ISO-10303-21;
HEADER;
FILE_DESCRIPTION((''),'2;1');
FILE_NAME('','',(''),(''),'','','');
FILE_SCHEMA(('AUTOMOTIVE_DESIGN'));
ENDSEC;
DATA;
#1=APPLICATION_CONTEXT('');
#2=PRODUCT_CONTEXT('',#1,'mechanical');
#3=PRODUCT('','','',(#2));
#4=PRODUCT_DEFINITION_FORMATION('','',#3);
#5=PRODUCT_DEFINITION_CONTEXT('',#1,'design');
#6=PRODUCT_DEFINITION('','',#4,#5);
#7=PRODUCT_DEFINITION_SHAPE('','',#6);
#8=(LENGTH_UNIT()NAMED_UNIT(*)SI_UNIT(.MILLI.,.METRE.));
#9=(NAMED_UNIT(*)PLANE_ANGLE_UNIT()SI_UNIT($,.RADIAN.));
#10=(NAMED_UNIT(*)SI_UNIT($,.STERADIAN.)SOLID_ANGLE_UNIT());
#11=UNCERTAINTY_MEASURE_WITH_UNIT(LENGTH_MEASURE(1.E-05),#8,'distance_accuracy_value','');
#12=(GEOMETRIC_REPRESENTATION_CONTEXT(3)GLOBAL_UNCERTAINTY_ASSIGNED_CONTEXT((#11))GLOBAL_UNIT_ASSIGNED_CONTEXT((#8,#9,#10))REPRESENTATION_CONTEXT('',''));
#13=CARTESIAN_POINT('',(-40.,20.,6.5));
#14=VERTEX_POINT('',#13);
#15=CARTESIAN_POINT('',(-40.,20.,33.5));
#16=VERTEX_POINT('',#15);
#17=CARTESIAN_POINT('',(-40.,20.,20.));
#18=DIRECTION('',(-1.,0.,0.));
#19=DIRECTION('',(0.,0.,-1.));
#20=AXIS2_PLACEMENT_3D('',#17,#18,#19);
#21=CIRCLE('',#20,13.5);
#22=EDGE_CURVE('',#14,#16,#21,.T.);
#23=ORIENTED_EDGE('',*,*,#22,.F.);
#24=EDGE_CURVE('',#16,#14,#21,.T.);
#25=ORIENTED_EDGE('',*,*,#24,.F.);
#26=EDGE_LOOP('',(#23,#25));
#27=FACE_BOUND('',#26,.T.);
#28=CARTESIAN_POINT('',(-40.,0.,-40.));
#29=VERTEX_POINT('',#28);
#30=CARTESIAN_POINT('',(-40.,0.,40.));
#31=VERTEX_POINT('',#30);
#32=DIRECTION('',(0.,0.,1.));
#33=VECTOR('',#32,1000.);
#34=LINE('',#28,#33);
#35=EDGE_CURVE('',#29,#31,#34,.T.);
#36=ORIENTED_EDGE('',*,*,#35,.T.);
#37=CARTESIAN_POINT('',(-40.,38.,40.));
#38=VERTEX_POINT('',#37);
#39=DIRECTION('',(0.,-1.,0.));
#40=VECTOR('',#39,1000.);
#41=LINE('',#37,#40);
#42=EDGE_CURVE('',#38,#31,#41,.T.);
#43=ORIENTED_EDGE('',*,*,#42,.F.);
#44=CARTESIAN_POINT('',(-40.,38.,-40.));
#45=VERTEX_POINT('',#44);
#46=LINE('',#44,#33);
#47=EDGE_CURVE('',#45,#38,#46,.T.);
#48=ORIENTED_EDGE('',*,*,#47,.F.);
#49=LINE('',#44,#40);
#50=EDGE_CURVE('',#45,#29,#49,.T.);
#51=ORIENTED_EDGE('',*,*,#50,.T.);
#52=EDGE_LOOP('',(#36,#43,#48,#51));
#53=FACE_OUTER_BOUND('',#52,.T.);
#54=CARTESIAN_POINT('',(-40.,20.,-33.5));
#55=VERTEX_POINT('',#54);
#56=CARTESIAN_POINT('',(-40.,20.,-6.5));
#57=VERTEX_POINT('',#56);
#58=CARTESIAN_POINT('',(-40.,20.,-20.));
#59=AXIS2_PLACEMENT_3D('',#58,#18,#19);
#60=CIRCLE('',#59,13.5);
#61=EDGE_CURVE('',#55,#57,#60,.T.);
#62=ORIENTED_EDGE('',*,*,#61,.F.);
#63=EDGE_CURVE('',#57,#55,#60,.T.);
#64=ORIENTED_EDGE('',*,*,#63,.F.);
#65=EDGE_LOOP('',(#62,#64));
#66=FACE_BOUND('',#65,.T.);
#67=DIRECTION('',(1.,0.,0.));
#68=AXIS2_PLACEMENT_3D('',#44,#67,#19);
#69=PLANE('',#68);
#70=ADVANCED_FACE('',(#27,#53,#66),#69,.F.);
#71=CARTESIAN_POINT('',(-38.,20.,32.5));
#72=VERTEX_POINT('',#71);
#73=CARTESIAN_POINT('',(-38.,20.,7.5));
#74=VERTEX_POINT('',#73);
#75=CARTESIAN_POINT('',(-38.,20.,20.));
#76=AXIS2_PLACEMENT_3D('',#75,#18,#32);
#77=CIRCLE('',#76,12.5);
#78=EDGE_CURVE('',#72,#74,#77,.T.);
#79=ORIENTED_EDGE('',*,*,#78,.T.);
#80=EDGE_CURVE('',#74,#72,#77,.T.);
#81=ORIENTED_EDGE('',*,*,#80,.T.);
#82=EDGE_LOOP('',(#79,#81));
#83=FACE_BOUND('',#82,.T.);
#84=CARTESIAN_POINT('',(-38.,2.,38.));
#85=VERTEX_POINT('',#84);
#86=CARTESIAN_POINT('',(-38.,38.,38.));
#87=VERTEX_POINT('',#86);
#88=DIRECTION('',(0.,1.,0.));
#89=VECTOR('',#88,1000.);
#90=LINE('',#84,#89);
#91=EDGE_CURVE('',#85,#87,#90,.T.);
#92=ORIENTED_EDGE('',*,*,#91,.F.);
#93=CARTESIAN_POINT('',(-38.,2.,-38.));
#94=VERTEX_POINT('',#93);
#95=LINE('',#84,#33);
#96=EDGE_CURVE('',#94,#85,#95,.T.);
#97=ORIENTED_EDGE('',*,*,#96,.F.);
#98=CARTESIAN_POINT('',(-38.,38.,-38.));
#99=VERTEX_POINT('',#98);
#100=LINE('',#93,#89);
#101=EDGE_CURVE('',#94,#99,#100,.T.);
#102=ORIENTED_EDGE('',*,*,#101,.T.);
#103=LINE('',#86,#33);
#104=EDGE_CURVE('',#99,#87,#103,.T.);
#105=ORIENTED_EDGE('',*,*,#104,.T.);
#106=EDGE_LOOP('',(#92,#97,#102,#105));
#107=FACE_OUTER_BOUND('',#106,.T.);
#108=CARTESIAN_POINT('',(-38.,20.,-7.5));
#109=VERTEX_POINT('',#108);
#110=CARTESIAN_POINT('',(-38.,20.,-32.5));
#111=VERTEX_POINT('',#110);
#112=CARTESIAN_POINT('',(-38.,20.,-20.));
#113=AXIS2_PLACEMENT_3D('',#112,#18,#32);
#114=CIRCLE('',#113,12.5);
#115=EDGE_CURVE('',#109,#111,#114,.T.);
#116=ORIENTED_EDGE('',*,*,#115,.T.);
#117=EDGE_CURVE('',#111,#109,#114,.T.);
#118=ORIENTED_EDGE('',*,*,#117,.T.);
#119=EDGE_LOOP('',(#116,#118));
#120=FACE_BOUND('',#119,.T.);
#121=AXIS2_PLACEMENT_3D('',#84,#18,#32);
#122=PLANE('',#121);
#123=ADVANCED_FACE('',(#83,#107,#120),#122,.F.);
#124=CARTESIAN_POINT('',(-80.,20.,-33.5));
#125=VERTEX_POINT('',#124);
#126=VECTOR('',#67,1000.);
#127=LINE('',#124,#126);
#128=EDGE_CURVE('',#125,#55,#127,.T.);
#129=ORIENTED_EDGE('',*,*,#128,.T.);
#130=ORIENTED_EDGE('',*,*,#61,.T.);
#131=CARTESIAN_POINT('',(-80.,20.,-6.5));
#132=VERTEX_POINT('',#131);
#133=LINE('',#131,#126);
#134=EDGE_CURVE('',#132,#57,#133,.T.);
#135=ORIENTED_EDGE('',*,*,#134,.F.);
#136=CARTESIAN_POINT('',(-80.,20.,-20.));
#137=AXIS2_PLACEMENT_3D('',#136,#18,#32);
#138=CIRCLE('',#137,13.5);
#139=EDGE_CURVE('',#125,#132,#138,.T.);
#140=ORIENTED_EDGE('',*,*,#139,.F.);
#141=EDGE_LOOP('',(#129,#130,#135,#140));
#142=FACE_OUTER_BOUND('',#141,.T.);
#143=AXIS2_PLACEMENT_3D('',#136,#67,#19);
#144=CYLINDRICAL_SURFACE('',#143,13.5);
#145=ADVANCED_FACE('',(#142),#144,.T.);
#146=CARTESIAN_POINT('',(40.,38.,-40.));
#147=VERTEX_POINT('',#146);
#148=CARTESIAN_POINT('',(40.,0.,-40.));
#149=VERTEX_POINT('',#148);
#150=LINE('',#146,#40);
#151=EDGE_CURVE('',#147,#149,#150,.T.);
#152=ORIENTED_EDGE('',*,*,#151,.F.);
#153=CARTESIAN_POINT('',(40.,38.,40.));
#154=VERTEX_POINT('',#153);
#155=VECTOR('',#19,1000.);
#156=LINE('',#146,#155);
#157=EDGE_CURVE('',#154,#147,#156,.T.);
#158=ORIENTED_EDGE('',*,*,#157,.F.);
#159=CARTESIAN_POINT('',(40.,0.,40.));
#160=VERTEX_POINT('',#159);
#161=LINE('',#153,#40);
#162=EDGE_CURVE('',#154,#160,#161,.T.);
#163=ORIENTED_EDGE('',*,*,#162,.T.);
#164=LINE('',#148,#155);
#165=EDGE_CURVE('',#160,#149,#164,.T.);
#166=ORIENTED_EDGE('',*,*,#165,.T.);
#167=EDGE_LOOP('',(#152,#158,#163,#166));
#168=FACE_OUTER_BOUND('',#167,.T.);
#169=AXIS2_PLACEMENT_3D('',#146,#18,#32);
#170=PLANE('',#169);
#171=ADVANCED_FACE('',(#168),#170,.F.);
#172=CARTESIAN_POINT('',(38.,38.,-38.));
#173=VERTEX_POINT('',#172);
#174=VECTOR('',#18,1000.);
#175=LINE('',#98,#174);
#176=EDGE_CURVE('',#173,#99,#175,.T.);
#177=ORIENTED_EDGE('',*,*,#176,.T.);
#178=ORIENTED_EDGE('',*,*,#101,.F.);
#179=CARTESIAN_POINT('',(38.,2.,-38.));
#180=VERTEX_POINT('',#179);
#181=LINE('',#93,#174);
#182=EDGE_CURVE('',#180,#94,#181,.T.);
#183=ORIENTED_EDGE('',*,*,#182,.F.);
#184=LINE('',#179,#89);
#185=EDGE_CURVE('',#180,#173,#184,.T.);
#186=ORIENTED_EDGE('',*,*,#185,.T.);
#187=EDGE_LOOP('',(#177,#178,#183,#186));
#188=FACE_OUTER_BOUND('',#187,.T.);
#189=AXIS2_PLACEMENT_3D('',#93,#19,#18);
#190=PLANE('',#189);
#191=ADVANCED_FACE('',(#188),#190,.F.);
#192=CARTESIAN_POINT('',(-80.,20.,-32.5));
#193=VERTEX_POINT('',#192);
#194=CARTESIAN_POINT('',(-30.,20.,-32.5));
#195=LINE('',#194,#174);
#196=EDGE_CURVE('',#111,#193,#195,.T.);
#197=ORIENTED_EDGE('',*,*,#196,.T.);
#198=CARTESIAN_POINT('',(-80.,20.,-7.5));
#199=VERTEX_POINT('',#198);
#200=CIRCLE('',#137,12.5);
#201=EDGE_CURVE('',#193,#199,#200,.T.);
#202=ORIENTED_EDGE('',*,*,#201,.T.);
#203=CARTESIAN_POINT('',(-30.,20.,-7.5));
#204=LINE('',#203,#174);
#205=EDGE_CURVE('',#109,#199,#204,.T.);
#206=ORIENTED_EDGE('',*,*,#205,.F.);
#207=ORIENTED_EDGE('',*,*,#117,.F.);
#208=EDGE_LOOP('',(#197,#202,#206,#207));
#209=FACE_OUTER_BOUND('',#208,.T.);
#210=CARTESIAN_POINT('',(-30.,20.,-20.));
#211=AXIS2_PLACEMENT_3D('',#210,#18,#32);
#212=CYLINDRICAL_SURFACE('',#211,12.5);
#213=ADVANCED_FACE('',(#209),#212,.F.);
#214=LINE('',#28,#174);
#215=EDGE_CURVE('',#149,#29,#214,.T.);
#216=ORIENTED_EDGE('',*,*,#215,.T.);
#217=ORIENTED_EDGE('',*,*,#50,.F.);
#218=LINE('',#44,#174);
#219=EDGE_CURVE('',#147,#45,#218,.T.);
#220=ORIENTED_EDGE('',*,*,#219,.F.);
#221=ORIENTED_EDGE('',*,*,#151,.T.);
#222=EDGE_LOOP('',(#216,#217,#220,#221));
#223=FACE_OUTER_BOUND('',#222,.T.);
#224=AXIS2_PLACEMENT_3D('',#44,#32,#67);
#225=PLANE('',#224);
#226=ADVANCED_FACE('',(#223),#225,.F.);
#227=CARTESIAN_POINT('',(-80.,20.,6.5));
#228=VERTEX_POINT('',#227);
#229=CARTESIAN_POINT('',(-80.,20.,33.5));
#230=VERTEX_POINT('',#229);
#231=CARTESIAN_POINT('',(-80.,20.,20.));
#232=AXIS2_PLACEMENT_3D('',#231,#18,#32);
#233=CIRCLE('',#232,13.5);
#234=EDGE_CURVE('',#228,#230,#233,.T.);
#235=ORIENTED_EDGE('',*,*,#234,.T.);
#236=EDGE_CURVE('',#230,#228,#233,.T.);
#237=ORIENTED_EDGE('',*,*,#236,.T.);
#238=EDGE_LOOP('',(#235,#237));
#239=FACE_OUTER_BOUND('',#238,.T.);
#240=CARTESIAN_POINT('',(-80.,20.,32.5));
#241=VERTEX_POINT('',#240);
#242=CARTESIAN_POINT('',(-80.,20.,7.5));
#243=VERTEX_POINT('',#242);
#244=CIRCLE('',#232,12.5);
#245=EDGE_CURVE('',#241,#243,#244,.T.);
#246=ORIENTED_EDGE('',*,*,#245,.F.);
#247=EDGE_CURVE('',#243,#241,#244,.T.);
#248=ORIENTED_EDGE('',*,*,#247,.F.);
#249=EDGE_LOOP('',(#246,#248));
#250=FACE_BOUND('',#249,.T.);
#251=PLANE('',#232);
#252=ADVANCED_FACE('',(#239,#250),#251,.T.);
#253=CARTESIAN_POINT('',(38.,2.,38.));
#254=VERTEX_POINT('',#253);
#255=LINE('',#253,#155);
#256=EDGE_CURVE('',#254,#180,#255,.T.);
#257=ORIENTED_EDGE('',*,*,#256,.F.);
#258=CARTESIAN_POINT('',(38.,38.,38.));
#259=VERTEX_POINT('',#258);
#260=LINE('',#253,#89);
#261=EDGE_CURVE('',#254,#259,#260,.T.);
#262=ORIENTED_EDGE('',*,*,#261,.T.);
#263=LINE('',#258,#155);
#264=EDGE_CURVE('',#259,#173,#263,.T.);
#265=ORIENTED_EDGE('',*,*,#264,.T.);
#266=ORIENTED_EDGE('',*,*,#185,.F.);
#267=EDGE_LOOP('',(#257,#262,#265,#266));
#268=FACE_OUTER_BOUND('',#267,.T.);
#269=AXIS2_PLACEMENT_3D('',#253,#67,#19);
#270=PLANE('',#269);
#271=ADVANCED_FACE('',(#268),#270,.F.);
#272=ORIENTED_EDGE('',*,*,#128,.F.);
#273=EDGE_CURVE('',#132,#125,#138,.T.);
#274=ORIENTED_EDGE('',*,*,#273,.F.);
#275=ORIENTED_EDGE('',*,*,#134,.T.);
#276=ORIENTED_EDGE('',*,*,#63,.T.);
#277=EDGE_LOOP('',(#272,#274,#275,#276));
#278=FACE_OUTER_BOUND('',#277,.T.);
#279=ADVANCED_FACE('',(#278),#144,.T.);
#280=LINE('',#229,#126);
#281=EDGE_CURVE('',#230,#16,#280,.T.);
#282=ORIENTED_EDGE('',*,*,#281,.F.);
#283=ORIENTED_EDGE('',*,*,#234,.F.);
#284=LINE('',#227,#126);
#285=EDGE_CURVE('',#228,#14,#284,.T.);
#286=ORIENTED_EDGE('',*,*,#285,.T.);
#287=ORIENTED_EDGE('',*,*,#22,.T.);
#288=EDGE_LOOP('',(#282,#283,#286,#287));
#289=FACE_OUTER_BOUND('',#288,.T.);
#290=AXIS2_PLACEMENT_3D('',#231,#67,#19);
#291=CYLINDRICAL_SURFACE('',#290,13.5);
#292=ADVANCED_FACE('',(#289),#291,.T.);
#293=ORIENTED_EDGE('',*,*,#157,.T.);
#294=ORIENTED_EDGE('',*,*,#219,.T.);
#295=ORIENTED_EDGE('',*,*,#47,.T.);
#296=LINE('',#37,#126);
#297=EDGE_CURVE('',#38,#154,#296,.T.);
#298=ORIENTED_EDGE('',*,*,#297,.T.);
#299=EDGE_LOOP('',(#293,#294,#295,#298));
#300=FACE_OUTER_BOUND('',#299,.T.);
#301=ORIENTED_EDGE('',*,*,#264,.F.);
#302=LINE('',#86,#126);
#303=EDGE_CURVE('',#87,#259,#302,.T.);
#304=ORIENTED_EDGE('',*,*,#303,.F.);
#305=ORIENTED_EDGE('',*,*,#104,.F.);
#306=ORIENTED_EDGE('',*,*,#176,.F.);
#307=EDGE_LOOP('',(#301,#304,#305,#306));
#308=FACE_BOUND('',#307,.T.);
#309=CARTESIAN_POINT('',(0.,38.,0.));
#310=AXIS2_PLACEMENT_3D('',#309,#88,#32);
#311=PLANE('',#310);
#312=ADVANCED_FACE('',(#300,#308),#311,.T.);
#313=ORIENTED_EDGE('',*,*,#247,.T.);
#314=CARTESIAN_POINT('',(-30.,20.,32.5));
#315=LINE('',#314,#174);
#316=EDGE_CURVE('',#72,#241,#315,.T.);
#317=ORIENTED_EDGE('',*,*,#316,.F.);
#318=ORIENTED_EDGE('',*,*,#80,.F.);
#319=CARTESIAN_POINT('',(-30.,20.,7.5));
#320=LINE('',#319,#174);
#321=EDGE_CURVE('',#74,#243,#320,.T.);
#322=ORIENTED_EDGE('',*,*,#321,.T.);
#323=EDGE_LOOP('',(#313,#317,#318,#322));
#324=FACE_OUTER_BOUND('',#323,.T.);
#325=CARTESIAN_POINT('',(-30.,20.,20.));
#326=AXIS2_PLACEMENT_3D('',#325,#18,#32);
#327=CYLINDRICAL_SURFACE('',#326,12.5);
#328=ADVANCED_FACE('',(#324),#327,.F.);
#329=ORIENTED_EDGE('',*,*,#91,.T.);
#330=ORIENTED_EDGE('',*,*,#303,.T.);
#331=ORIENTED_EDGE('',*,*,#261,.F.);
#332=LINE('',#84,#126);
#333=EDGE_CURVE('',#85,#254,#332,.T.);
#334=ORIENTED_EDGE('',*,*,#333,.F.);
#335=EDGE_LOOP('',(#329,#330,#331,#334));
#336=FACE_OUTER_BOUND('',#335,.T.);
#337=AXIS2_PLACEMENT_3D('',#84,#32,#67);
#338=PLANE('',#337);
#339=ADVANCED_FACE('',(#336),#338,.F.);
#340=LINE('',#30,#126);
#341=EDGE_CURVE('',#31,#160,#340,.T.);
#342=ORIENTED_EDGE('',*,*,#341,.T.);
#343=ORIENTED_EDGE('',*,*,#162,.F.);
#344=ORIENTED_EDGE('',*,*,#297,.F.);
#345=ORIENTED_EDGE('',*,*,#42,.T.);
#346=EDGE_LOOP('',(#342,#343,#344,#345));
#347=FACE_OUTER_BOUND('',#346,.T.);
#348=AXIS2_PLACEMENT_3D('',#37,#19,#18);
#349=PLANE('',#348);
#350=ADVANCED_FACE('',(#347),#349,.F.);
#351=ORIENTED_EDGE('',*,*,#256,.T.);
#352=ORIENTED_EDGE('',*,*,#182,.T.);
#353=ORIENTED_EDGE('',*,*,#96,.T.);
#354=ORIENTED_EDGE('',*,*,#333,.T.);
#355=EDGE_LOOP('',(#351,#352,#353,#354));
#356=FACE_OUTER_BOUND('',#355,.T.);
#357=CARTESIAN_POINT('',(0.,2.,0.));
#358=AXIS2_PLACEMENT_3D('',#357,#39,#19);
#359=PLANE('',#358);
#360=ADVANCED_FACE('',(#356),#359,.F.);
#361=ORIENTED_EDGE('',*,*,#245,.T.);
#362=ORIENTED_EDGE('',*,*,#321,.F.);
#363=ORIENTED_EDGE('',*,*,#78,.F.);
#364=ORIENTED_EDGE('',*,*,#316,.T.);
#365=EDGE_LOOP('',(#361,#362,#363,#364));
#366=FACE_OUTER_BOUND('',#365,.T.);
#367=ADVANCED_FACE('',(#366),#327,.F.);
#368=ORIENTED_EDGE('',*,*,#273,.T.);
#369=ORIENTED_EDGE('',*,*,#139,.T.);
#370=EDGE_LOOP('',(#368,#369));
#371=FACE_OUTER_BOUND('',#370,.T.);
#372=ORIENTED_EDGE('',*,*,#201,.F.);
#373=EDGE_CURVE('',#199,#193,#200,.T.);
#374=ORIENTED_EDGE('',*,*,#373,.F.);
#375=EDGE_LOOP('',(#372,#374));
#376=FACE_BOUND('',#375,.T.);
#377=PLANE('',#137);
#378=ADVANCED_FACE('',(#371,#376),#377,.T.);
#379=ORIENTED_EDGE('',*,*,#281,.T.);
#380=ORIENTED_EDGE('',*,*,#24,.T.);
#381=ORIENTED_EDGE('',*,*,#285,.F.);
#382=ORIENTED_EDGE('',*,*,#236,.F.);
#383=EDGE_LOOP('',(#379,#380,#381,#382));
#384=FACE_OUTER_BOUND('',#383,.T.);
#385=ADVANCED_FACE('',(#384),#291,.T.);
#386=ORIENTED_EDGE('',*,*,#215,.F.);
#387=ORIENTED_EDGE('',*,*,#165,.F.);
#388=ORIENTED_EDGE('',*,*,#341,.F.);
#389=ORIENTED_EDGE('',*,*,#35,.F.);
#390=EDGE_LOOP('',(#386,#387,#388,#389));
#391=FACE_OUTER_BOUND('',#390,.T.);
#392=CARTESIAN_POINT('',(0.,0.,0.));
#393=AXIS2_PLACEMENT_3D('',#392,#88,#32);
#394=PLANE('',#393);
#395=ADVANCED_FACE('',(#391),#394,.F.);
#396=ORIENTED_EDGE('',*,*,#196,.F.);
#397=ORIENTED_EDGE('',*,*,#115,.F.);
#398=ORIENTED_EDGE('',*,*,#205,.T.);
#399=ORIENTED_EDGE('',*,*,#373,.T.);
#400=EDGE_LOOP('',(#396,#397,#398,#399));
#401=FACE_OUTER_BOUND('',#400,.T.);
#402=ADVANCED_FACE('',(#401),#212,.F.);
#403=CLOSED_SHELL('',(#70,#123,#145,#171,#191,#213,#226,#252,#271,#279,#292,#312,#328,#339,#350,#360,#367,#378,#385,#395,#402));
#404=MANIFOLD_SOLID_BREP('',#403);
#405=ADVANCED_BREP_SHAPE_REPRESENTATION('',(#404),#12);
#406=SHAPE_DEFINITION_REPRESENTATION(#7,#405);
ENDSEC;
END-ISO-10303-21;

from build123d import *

# Parameters (mm, degrees)
SKETCH1_W           = 80
SKETCH1_H           = 80
BOSS_EXTRUDE1_DEPTH = 38
SKETCH2_W           = 76
SKETCH2_H           = 76
CUT_EXTRUDE1_DEPTH  = 36
SKETCH3_R           = 12.5
CUT_EXTRUDE2_DEPTH  = 10
BOSS_EXTRUDE3_START = 40
SKETCH4_R           = 13.5
SKETCH4_R_2         = 12.5
BOSS_EXTRUDE3_DEPTH = 40


with BuildPart() as part:
    # Sketch1 → Boss-Extrude1 (new body)
    with BuildSketch(Plane(origin=(0, 0, 0), x_dir=(1, 0, 0), z_dir=(0, 1, 0))):
        Rectangle(SKETCH1_W, SKETCH1_H)
    extrude(amount=BOSS_EXTRUDE1_DEPTH)

    # Sketch2 → Cut-Extrude1 (cut)
    with BuildSketch(Plane(origin=(0, 38, 0), x_dir=(1, 0, 0), z_dir=(0, 1, 0))):
        Rectangle(SKETCH2_W, SKETCH2_H)
    extrude(amount=-CUT_EXTRUDE1_DEPTH, mode=Mode.SUBTRACT)

    # Sketch3 → Cut-Extrude2 (cut)
    with BuildSketch(Plane.ZY.offset(40)):
        with Locations((-20, 20)):
            Circle(SKETCH3_R)
        with Locations((20, 20)):
            Circle(SKETCH3_R)
    extrude(amount=-CUT_EXTRUDE2_DEPTH, mode=Mode.SUBTRACT)

    # Sketch4 → Boss-Extrude3 (add)
    # profile 1 of 2: a face of its own
    with BuildSketch(Plane.ZY.offset(40).offset(BOSS_EXTRUDE3_START)):
        with Locations(Location((-20, 20, 0), (0, 0, 180))):
            Circle(SKETCH4_R)
        with Locations((-20, 20)):
            Circle(SKETCH4_R_2, mode=Mode.SUBTRACT)
    # profile 2 of 2: a face of its own
    with BuildSketch(Plane.ZY.offset(40).offset(BOSS_EXTRUDE3_START)):
        with Locations(Location((20, 20, 0), (0, 0, 180))):
            Circle(SKETCH4_R)
        with Locations((20, 20)):
            Circle(SKETCH4_R_2, mode=Mode.SUBTRACT)
    extrude(amount=-BOSS_EXTRUDE3_DEPTH)


solid = part.part
